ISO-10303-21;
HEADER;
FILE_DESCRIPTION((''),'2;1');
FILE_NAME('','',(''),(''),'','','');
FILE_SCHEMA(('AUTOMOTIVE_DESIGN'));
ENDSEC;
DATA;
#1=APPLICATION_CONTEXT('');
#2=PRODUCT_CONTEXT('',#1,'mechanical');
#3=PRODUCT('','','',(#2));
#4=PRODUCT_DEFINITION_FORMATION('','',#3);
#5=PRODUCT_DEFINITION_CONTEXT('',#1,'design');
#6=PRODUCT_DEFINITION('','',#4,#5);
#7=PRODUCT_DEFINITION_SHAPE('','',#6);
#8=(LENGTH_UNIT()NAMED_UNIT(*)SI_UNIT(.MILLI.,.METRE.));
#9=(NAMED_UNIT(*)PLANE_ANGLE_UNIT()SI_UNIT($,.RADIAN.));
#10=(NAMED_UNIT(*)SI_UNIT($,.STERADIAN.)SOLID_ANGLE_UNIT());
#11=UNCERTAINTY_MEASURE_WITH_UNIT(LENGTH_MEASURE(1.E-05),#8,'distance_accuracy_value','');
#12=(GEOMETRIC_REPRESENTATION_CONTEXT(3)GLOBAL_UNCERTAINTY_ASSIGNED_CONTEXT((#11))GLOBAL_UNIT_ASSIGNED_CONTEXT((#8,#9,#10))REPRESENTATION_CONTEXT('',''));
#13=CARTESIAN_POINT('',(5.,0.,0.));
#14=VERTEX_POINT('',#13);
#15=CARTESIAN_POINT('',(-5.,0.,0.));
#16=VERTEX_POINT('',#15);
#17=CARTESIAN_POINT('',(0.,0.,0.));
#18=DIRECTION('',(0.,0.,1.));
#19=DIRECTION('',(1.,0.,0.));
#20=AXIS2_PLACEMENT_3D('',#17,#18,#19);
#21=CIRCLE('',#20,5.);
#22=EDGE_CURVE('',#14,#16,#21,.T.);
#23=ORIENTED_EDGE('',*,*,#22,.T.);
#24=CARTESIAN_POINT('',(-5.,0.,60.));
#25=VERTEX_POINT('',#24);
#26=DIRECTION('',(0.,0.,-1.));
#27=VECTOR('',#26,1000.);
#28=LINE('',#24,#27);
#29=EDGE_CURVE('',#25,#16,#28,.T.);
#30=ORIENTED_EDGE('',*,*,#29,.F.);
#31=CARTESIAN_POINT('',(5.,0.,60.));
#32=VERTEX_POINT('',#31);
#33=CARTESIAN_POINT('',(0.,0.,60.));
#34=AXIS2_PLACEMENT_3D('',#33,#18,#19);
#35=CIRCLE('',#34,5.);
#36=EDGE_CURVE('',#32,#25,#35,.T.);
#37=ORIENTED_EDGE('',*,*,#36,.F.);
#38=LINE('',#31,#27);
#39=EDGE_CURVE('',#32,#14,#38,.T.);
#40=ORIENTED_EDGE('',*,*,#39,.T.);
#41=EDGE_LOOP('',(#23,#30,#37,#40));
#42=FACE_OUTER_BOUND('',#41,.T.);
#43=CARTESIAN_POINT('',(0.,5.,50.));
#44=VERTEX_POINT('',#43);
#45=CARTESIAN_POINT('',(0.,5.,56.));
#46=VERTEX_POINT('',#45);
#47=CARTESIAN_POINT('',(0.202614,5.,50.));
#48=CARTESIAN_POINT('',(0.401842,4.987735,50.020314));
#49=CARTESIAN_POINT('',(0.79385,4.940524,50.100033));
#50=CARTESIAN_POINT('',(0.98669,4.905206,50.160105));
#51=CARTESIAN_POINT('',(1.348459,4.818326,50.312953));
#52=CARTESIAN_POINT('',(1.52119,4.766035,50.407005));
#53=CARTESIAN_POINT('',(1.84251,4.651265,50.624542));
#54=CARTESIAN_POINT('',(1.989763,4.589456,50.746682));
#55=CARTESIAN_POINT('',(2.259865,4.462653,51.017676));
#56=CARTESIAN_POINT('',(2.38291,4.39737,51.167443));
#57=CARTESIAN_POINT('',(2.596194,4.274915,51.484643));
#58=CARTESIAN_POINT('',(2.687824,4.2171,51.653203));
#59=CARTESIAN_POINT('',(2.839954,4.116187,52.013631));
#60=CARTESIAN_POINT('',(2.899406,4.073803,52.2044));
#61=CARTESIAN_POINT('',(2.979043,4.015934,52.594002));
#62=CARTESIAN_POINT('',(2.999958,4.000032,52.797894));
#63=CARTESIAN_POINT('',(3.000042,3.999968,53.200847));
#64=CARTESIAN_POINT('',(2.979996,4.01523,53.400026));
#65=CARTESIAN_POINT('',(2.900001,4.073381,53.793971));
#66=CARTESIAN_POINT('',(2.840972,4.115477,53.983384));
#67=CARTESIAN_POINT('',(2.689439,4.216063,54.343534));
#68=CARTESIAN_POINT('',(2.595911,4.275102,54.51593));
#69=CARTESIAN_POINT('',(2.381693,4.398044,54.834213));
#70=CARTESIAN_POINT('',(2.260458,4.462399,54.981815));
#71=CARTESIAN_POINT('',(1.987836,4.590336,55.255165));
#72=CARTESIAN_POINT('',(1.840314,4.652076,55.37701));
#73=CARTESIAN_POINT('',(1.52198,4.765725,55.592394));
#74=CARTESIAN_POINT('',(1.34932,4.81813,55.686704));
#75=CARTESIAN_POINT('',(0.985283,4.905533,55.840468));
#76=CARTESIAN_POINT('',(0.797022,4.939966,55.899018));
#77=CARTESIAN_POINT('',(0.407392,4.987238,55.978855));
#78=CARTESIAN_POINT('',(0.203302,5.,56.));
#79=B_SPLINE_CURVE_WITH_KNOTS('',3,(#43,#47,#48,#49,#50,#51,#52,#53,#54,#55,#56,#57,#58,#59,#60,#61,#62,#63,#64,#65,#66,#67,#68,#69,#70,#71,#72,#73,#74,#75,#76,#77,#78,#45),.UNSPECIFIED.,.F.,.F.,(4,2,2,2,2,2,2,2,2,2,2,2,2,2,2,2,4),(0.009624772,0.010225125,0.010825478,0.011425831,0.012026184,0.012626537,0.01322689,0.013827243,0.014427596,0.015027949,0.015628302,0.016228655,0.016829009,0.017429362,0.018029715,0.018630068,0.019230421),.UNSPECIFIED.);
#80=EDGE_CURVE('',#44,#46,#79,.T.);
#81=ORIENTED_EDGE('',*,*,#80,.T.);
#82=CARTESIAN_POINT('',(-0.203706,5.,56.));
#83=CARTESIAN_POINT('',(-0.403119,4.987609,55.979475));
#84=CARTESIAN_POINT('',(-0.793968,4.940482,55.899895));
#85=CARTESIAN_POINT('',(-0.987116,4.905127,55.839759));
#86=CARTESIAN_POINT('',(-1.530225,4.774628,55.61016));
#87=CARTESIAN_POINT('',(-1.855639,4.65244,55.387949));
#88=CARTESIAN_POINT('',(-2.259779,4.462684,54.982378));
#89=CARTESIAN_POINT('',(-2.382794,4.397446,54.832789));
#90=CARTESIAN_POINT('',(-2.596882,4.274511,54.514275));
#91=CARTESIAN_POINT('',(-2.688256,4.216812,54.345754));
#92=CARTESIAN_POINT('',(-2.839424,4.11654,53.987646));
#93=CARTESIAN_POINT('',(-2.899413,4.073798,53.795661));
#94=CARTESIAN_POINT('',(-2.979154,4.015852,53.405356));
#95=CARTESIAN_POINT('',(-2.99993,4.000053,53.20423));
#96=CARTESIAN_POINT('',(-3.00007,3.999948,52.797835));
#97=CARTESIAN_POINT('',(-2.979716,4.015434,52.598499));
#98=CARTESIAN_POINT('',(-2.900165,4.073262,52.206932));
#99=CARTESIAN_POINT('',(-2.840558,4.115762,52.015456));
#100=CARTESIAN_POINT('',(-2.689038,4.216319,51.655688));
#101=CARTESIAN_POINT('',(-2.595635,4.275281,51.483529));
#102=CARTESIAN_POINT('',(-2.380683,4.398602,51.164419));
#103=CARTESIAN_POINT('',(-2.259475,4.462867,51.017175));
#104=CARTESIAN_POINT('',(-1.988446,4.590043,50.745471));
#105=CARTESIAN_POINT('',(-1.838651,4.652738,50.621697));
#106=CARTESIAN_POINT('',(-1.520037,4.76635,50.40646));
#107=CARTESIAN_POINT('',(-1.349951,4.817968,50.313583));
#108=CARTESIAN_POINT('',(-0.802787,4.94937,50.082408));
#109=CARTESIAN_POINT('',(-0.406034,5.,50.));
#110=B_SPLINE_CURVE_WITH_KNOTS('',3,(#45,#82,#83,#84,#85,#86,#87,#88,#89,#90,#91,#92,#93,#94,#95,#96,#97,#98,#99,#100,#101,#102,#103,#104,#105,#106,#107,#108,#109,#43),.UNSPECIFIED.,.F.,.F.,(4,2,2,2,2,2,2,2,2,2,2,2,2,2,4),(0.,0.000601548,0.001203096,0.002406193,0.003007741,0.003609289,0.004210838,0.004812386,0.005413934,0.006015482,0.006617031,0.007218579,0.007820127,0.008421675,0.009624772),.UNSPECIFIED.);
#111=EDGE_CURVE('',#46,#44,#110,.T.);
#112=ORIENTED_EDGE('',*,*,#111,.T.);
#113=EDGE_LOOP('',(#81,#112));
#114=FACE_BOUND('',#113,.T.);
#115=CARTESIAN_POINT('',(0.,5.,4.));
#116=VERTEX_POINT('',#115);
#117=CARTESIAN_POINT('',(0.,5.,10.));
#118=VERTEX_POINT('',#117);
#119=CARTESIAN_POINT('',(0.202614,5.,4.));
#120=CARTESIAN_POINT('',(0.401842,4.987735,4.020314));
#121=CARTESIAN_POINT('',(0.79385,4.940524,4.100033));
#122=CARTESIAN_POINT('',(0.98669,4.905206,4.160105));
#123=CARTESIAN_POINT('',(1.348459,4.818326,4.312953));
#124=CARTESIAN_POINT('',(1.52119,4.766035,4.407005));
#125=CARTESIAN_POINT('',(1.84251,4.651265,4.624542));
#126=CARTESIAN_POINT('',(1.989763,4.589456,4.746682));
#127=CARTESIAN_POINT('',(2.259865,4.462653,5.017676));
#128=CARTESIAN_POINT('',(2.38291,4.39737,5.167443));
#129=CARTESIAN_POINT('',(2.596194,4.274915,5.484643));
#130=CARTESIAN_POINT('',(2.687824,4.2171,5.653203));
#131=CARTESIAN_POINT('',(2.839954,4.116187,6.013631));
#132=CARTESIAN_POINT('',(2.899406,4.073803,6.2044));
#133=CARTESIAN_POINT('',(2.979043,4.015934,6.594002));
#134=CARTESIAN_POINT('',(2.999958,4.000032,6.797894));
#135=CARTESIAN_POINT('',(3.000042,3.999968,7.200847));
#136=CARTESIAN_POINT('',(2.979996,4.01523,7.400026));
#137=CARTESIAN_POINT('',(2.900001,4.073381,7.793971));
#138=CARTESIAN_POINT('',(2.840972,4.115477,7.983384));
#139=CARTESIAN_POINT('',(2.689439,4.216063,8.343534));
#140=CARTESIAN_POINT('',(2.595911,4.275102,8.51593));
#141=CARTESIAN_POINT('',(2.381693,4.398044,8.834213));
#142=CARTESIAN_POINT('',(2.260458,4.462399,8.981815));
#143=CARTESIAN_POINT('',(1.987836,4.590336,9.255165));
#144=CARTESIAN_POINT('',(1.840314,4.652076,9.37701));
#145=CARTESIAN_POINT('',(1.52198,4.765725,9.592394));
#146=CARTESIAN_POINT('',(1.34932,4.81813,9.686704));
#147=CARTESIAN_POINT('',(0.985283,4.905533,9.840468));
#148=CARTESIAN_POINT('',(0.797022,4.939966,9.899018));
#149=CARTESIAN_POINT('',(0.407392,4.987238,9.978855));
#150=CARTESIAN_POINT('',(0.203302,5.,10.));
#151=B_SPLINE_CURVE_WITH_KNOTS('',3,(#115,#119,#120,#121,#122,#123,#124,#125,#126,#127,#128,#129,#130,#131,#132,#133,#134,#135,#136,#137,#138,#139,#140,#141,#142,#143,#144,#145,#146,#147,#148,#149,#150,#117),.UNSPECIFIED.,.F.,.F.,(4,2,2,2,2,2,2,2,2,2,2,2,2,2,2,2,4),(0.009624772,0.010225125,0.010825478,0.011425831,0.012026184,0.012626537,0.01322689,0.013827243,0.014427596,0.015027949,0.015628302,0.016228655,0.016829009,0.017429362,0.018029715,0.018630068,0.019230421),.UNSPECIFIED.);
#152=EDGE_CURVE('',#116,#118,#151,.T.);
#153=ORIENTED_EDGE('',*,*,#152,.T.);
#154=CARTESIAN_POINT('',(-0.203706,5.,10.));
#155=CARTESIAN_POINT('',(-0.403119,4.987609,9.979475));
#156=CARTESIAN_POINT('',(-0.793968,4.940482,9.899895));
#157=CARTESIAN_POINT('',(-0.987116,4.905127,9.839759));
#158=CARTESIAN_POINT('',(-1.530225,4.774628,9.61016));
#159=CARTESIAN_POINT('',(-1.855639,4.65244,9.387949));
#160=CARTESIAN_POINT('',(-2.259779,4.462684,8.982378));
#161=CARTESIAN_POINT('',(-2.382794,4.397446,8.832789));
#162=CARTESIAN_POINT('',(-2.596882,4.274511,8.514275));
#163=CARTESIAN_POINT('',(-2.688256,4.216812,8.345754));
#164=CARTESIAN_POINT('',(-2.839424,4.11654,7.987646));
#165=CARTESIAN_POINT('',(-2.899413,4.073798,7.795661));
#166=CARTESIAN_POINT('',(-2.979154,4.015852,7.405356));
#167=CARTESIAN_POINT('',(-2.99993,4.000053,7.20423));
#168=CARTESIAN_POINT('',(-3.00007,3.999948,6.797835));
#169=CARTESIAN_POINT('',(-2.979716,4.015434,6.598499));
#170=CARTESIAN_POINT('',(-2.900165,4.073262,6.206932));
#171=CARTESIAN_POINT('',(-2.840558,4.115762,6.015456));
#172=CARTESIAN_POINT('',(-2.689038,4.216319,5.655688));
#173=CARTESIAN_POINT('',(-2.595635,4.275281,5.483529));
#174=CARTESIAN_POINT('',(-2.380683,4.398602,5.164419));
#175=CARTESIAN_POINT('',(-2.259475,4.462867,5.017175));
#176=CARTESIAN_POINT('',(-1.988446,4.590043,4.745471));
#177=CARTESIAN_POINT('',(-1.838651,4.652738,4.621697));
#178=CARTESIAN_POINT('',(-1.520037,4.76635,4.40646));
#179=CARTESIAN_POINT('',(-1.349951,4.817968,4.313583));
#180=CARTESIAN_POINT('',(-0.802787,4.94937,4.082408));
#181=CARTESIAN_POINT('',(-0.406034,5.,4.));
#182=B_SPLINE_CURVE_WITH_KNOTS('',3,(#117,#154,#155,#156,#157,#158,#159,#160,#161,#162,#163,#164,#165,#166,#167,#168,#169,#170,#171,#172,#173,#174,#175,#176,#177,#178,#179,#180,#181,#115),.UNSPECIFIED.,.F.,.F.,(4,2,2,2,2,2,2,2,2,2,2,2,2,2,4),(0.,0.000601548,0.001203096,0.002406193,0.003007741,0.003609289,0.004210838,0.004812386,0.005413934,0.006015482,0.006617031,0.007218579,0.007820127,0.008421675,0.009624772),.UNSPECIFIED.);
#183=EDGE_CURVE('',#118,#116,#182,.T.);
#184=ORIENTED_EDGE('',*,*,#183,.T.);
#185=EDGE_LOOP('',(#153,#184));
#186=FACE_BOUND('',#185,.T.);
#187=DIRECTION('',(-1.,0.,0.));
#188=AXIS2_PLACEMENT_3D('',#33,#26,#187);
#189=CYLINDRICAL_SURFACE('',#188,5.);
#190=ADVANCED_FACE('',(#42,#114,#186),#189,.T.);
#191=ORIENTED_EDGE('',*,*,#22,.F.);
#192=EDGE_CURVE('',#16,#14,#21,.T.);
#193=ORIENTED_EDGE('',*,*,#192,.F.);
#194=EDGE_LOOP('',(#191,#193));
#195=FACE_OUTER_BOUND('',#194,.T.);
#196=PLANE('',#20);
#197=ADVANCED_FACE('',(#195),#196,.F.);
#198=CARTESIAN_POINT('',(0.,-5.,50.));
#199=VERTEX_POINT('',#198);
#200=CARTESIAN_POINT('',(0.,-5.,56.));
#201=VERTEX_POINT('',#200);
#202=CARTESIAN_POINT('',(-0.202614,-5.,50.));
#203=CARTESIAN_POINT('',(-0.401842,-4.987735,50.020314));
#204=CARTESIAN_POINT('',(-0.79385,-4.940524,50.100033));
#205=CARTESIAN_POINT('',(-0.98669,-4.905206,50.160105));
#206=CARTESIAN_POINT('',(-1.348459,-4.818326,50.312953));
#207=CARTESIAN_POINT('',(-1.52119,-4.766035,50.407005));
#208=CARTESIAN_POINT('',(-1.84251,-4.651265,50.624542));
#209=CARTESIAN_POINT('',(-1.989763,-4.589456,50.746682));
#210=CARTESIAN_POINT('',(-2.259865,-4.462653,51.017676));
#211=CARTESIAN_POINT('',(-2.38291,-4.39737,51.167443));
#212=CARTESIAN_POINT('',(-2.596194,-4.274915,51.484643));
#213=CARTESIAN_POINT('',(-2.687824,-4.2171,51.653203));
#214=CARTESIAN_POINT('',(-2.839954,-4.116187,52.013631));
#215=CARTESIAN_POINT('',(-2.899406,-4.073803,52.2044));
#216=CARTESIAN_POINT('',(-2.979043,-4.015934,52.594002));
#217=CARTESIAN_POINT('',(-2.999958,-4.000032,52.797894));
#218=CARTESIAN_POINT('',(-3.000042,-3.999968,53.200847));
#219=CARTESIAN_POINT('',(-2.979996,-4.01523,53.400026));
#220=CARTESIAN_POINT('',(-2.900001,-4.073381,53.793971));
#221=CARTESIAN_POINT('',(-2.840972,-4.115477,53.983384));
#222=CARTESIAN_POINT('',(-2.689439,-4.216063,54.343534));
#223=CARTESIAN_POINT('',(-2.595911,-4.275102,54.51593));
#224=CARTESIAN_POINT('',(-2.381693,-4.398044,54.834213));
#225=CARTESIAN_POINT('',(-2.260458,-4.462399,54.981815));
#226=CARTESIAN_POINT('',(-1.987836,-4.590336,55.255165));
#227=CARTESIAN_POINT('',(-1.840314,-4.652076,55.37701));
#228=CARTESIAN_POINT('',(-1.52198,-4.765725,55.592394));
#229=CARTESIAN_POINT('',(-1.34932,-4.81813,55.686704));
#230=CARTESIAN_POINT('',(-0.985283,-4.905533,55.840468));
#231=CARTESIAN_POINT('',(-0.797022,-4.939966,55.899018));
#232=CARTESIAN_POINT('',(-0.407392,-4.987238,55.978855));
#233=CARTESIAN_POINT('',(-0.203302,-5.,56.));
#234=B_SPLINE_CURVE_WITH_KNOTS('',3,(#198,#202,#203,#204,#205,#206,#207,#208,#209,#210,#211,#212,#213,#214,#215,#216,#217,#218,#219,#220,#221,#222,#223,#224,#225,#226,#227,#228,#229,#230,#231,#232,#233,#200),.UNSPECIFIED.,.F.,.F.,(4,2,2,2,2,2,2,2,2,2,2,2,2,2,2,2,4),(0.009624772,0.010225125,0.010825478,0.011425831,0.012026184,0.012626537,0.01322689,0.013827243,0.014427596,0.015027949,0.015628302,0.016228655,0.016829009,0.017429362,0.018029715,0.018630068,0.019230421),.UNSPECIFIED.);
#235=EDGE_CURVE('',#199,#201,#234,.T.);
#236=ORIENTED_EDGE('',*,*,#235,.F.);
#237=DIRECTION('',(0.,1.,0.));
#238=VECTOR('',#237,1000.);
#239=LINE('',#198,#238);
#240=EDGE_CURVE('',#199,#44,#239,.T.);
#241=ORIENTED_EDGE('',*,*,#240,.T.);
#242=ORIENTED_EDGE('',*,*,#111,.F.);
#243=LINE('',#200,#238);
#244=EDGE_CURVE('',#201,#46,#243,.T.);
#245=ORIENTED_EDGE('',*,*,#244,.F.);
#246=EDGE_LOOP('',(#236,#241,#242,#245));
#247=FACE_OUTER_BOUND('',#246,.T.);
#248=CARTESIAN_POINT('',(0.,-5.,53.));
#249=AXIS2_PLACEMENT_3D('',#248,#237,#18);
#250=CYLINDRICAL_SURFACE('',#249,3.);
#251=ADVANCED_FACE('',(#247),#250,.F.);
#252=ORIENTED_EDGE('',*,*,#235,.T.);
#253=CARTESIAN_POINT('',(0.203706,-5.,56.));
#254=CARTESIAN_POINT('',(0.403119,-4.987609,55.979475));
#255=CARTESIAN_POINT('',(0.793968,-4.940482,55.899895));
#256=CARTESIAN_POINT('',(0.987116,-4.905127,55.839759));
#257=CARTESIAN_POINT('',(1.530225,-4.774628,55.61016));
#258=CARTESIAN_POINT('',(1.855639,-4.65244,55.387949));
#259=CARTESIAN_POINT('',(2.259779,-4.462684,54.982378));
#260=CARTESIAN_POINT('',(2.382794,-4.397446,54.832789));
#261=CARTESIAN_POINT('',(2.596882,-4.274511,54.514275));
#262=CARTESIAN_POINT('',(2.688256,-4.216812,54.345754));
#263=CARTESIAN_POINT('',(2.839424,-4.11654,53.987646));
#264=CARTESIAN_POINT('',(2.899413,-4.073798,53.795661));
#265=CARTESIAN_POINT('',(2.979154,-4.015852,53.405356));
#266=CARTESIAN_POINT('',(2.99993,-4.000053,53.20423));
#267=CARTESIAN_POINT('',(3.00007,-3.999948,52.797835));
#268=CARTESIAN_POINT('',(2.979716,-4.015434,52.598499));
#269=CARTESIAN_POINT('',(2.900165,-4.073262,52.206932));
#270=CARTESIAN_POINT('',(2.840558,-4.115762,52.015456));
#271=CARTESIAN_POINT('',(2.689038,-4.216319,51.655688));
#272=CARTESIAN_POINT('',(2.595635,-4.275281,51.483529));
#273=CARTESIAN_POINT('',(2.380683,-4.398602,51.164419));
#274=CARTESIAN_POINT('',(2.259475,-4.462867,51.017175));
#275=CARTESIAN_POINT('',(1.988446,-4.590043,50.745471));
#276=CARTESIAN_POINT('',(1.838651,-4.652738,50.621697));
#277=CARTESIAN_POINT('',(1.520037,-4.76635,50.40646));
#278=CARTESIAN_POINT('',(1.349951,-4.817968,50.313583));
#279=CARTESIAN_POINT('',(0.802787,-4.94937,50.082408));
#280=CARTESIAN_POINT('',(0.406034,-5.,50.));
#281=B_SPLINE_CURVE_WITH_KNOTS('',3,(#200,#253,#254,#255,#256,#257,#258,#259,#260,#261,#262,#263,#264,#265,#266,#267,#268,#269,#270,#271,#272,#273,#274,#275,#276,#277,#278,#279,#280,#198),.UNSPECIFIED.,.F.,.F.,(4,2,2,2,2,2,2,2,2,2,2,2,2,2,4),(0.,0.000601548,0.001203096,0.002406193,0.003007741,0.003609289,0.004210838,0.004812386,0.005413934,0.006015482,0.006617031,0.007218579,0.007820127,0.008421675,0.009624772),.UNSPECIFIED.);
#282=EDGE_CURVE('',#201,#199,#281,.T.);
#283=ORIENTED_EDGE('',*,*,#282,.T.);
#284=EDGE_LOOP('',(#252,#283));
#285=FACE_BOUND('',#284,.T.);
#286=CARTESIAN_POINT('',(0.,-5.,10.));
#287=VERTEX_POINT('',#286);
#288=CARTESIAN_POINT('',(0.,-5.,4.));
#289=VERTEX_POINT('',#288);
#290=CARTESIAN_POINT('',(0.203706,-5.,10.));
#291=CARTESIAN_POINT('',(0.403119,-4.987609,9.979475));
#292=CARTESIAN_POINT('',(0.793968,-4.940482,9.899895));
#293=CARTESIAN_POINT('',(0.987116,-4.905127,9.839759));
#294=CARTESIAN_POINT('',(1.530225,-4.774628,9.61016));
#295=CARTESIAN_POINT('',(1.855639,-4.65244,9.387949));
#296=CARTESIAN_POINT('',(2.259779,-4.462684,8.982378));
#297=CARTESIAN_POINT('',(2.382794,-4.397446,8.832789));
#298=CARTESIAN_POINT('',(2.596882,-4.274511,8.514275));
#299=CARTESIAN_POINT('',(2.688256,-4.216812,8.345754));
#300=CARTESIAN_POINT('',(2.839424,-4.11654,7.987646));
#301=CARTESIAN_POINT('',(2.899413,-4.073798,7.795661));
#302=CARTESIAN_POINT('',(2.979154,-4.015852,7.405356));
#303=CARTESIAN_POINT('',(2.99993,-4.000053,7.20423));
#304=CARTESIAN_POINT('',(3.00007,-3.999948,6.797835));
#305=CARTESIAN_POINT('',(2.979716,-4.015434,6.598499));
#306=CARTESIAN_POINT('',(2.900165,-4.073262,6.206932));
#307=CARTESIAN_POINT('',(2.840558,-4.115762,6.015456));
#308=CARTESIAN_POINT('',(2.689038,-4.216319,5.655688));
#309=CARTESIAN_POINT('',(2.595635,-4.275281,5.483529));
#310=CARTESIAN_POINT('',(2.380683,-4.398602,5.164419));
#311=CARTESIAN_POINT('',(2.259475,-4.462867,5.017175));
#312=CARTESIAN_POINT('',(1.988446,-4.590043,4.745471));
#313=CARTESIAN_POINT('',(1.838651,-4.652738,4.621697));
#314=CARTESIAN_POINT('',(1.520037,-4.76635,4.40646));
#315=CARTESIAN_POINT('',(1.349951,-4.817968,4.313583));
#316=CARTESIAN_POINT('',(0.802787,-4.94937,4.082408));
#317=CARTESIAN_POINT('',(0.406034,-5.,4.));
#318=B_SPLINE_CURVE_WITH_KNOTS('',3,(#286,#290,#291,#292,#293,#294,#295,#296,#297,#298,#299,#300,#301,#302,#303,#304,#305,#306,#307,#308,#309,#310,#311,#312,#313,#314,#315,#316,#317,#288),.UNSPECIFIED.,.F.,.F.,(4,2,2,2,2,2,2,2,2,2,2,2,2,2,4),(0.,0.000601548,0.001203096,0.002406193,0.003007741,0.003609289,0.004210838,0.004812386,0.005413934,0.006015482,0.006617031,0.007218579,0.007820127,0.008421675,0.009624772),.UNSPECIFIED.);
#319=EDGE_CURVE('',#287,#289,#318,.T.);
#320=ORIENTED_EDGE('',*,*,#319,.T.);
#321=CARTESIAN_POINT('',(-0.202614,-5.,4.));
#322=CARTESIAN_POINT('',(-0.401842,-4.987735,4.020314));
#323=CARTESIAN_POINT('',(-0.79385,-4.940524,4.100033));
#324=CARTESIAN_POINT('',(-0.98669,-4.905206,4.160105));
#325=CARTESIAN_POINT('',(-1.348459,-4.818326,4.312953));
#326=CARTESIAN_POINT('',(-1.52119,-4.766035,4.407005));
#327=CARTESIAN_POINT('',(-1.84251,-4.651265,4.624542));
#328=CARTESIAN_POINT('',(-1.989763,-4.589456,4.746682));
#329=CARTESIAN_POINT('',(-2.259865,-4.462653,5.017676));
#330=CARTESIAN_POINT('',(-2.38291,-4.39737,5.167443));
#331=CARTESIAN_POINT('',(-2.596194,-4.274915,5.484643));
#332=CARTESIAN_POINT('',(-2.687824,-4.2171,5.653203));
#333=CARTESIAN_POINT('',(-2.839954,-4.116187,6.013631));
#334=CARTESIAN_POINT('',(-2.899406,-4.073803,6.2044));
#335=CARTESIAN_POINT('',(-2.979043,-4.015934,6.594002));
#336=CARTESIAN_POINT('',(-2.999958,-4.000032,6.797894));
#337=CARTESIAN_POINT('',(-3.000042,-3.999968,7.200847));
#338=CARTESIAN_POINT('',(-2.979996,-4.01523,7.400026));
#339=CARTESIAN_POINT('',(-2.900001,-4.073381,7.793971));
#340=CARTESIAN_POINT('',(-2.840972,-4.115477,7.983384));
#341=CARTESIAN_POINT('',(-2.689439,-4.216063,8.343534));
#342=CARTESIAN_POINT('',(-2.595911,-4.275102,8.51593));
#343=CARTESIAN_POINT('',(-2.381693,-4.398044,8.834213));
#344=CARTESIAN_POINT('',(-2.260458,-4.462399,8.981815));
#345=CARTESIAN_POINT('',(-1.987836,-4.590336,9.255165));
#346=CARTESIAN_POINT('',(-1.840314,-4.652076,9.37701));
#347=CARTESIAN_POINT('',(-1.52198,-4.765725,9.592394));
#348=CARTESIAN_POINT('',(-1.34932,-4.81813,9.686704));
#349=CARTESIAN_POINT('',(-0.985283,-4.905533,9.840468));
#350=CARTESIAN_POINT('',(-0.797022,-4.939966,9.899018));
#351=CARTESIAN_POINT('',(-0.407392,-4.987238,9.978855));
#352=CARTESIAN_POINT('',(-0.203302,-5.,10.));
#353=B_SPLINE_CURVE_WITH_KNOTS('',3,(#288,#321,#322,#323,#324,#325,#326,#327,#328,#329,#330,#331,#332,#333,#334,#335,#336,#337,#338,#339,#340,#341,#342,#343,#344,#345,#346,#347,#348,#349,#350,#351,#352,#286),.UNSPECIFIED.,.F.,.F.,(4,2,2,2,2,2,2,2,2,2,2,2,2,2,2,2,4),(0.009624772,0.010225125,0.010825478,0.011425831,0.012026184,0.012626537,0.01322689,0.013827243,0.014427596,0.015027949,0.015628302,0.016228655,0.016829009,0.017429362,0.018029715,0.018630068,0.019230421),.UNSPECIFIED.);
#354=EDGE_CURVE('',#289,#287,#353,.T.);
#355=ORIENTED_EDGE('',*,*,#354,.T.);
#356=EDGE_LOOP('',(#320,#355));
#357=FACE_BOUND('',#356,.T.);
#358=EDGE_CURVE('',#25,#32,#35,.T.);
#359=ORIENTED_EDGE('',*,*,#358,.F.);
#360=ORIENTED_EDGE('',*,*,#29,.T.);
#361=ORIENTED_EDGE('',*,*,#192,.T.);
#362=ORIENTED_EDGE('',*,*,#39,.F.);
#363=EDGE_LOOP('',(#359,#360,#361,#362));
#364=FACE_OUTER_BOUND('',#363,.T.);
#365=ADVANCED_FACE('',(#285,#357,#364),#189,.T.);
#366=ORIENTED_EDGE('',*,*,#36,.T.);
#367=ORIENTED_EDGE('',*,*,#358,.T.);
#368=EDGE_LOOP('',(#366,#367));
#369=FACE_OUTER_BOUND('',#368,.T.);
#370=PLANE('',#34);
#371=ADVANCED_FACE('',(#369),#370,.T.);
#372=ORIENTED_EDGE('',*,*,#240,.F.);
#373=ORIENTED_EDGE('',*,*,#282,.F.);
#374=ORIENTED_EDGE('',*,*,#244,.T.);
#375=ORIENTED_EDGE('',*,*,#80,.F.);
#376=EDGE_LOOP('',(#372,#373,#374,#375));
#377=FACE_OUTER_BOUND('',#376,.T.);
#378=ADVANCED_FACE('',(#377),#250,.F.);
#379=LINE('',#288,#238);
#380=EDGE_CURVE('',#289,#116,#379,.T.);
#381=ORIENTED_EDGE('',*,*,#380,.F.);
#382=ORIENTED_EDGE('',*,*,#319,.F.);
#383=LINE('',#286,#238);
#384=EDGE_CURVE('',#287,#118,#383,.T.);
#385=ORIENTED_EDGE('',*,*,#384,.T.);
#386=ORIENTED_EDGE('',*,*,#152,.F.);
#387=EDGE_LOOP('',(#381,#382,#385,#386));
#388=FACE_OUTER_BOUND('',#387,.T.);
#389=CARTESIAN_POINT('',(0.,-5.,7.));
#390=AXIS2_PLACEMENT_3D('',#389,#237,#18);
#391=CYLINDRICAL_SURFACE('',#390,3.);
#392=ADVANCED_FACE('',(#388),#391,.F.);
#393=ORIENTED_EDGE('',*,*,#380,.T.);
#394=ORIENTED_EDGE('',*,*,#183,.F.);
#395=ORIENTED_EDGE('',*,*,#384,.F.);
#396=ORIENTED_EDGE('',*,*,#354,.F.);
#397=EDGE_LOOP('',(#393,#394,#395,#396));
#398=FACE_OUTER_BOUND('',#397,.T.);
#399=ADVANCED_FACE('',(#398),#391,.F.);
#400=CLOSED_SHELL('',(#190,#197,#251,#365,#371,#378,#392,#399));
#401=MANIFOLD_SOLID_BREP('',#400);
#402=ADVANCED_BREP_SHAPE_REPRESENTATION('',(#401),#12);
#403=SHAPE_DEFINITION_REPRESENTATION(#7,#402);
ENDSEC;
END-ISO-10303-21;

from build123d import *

# Parameters (mm, degrees)
SKETCH1_R               = 5
BOSS_EXTRUDE1_DEPTH     = 60
CUT_EXTRUDE1_DEPTH      = 61.415229868
CUT_EXTRUDE1_DEPTH_BACK = 61.415229868
SKETCH2_R               = 3


with BuildPart() as part:
    # Sketch1 → Boss-Extrude1 (new body)
    with BuildSketch(Plane.XY):
        Circle(SKETCH1_R)
    extrude(amount=BOSS_EXTRUDE1_DEPTH)

    # Sketch2 → Cut-Extrude1 (cut, two sides: drawn at the far end of the back side and taken through both)
    with BuildSketch(Plane(origin=(0, 0, 0), x_dir=(1, 0, 0), z_dir=(0, 1, 0)).offset(-CUT_EXTRUDE1_DEPTH_BACK)):
        with Locations(Location((0, -7, 0), (0, 0, 270))):
            Circle(SKETCH2_R)
        with Locations(Location((0, -53, 0), (0, 0, 270))):
            Circle(SKETCH2_R)
    extrude(amount=CUT_EXTRUDE1_DEPTH + CUT_EXTRUDE1_DEPTH_BACK, mode=Mode.SUBTRACT)


solid = part.part
